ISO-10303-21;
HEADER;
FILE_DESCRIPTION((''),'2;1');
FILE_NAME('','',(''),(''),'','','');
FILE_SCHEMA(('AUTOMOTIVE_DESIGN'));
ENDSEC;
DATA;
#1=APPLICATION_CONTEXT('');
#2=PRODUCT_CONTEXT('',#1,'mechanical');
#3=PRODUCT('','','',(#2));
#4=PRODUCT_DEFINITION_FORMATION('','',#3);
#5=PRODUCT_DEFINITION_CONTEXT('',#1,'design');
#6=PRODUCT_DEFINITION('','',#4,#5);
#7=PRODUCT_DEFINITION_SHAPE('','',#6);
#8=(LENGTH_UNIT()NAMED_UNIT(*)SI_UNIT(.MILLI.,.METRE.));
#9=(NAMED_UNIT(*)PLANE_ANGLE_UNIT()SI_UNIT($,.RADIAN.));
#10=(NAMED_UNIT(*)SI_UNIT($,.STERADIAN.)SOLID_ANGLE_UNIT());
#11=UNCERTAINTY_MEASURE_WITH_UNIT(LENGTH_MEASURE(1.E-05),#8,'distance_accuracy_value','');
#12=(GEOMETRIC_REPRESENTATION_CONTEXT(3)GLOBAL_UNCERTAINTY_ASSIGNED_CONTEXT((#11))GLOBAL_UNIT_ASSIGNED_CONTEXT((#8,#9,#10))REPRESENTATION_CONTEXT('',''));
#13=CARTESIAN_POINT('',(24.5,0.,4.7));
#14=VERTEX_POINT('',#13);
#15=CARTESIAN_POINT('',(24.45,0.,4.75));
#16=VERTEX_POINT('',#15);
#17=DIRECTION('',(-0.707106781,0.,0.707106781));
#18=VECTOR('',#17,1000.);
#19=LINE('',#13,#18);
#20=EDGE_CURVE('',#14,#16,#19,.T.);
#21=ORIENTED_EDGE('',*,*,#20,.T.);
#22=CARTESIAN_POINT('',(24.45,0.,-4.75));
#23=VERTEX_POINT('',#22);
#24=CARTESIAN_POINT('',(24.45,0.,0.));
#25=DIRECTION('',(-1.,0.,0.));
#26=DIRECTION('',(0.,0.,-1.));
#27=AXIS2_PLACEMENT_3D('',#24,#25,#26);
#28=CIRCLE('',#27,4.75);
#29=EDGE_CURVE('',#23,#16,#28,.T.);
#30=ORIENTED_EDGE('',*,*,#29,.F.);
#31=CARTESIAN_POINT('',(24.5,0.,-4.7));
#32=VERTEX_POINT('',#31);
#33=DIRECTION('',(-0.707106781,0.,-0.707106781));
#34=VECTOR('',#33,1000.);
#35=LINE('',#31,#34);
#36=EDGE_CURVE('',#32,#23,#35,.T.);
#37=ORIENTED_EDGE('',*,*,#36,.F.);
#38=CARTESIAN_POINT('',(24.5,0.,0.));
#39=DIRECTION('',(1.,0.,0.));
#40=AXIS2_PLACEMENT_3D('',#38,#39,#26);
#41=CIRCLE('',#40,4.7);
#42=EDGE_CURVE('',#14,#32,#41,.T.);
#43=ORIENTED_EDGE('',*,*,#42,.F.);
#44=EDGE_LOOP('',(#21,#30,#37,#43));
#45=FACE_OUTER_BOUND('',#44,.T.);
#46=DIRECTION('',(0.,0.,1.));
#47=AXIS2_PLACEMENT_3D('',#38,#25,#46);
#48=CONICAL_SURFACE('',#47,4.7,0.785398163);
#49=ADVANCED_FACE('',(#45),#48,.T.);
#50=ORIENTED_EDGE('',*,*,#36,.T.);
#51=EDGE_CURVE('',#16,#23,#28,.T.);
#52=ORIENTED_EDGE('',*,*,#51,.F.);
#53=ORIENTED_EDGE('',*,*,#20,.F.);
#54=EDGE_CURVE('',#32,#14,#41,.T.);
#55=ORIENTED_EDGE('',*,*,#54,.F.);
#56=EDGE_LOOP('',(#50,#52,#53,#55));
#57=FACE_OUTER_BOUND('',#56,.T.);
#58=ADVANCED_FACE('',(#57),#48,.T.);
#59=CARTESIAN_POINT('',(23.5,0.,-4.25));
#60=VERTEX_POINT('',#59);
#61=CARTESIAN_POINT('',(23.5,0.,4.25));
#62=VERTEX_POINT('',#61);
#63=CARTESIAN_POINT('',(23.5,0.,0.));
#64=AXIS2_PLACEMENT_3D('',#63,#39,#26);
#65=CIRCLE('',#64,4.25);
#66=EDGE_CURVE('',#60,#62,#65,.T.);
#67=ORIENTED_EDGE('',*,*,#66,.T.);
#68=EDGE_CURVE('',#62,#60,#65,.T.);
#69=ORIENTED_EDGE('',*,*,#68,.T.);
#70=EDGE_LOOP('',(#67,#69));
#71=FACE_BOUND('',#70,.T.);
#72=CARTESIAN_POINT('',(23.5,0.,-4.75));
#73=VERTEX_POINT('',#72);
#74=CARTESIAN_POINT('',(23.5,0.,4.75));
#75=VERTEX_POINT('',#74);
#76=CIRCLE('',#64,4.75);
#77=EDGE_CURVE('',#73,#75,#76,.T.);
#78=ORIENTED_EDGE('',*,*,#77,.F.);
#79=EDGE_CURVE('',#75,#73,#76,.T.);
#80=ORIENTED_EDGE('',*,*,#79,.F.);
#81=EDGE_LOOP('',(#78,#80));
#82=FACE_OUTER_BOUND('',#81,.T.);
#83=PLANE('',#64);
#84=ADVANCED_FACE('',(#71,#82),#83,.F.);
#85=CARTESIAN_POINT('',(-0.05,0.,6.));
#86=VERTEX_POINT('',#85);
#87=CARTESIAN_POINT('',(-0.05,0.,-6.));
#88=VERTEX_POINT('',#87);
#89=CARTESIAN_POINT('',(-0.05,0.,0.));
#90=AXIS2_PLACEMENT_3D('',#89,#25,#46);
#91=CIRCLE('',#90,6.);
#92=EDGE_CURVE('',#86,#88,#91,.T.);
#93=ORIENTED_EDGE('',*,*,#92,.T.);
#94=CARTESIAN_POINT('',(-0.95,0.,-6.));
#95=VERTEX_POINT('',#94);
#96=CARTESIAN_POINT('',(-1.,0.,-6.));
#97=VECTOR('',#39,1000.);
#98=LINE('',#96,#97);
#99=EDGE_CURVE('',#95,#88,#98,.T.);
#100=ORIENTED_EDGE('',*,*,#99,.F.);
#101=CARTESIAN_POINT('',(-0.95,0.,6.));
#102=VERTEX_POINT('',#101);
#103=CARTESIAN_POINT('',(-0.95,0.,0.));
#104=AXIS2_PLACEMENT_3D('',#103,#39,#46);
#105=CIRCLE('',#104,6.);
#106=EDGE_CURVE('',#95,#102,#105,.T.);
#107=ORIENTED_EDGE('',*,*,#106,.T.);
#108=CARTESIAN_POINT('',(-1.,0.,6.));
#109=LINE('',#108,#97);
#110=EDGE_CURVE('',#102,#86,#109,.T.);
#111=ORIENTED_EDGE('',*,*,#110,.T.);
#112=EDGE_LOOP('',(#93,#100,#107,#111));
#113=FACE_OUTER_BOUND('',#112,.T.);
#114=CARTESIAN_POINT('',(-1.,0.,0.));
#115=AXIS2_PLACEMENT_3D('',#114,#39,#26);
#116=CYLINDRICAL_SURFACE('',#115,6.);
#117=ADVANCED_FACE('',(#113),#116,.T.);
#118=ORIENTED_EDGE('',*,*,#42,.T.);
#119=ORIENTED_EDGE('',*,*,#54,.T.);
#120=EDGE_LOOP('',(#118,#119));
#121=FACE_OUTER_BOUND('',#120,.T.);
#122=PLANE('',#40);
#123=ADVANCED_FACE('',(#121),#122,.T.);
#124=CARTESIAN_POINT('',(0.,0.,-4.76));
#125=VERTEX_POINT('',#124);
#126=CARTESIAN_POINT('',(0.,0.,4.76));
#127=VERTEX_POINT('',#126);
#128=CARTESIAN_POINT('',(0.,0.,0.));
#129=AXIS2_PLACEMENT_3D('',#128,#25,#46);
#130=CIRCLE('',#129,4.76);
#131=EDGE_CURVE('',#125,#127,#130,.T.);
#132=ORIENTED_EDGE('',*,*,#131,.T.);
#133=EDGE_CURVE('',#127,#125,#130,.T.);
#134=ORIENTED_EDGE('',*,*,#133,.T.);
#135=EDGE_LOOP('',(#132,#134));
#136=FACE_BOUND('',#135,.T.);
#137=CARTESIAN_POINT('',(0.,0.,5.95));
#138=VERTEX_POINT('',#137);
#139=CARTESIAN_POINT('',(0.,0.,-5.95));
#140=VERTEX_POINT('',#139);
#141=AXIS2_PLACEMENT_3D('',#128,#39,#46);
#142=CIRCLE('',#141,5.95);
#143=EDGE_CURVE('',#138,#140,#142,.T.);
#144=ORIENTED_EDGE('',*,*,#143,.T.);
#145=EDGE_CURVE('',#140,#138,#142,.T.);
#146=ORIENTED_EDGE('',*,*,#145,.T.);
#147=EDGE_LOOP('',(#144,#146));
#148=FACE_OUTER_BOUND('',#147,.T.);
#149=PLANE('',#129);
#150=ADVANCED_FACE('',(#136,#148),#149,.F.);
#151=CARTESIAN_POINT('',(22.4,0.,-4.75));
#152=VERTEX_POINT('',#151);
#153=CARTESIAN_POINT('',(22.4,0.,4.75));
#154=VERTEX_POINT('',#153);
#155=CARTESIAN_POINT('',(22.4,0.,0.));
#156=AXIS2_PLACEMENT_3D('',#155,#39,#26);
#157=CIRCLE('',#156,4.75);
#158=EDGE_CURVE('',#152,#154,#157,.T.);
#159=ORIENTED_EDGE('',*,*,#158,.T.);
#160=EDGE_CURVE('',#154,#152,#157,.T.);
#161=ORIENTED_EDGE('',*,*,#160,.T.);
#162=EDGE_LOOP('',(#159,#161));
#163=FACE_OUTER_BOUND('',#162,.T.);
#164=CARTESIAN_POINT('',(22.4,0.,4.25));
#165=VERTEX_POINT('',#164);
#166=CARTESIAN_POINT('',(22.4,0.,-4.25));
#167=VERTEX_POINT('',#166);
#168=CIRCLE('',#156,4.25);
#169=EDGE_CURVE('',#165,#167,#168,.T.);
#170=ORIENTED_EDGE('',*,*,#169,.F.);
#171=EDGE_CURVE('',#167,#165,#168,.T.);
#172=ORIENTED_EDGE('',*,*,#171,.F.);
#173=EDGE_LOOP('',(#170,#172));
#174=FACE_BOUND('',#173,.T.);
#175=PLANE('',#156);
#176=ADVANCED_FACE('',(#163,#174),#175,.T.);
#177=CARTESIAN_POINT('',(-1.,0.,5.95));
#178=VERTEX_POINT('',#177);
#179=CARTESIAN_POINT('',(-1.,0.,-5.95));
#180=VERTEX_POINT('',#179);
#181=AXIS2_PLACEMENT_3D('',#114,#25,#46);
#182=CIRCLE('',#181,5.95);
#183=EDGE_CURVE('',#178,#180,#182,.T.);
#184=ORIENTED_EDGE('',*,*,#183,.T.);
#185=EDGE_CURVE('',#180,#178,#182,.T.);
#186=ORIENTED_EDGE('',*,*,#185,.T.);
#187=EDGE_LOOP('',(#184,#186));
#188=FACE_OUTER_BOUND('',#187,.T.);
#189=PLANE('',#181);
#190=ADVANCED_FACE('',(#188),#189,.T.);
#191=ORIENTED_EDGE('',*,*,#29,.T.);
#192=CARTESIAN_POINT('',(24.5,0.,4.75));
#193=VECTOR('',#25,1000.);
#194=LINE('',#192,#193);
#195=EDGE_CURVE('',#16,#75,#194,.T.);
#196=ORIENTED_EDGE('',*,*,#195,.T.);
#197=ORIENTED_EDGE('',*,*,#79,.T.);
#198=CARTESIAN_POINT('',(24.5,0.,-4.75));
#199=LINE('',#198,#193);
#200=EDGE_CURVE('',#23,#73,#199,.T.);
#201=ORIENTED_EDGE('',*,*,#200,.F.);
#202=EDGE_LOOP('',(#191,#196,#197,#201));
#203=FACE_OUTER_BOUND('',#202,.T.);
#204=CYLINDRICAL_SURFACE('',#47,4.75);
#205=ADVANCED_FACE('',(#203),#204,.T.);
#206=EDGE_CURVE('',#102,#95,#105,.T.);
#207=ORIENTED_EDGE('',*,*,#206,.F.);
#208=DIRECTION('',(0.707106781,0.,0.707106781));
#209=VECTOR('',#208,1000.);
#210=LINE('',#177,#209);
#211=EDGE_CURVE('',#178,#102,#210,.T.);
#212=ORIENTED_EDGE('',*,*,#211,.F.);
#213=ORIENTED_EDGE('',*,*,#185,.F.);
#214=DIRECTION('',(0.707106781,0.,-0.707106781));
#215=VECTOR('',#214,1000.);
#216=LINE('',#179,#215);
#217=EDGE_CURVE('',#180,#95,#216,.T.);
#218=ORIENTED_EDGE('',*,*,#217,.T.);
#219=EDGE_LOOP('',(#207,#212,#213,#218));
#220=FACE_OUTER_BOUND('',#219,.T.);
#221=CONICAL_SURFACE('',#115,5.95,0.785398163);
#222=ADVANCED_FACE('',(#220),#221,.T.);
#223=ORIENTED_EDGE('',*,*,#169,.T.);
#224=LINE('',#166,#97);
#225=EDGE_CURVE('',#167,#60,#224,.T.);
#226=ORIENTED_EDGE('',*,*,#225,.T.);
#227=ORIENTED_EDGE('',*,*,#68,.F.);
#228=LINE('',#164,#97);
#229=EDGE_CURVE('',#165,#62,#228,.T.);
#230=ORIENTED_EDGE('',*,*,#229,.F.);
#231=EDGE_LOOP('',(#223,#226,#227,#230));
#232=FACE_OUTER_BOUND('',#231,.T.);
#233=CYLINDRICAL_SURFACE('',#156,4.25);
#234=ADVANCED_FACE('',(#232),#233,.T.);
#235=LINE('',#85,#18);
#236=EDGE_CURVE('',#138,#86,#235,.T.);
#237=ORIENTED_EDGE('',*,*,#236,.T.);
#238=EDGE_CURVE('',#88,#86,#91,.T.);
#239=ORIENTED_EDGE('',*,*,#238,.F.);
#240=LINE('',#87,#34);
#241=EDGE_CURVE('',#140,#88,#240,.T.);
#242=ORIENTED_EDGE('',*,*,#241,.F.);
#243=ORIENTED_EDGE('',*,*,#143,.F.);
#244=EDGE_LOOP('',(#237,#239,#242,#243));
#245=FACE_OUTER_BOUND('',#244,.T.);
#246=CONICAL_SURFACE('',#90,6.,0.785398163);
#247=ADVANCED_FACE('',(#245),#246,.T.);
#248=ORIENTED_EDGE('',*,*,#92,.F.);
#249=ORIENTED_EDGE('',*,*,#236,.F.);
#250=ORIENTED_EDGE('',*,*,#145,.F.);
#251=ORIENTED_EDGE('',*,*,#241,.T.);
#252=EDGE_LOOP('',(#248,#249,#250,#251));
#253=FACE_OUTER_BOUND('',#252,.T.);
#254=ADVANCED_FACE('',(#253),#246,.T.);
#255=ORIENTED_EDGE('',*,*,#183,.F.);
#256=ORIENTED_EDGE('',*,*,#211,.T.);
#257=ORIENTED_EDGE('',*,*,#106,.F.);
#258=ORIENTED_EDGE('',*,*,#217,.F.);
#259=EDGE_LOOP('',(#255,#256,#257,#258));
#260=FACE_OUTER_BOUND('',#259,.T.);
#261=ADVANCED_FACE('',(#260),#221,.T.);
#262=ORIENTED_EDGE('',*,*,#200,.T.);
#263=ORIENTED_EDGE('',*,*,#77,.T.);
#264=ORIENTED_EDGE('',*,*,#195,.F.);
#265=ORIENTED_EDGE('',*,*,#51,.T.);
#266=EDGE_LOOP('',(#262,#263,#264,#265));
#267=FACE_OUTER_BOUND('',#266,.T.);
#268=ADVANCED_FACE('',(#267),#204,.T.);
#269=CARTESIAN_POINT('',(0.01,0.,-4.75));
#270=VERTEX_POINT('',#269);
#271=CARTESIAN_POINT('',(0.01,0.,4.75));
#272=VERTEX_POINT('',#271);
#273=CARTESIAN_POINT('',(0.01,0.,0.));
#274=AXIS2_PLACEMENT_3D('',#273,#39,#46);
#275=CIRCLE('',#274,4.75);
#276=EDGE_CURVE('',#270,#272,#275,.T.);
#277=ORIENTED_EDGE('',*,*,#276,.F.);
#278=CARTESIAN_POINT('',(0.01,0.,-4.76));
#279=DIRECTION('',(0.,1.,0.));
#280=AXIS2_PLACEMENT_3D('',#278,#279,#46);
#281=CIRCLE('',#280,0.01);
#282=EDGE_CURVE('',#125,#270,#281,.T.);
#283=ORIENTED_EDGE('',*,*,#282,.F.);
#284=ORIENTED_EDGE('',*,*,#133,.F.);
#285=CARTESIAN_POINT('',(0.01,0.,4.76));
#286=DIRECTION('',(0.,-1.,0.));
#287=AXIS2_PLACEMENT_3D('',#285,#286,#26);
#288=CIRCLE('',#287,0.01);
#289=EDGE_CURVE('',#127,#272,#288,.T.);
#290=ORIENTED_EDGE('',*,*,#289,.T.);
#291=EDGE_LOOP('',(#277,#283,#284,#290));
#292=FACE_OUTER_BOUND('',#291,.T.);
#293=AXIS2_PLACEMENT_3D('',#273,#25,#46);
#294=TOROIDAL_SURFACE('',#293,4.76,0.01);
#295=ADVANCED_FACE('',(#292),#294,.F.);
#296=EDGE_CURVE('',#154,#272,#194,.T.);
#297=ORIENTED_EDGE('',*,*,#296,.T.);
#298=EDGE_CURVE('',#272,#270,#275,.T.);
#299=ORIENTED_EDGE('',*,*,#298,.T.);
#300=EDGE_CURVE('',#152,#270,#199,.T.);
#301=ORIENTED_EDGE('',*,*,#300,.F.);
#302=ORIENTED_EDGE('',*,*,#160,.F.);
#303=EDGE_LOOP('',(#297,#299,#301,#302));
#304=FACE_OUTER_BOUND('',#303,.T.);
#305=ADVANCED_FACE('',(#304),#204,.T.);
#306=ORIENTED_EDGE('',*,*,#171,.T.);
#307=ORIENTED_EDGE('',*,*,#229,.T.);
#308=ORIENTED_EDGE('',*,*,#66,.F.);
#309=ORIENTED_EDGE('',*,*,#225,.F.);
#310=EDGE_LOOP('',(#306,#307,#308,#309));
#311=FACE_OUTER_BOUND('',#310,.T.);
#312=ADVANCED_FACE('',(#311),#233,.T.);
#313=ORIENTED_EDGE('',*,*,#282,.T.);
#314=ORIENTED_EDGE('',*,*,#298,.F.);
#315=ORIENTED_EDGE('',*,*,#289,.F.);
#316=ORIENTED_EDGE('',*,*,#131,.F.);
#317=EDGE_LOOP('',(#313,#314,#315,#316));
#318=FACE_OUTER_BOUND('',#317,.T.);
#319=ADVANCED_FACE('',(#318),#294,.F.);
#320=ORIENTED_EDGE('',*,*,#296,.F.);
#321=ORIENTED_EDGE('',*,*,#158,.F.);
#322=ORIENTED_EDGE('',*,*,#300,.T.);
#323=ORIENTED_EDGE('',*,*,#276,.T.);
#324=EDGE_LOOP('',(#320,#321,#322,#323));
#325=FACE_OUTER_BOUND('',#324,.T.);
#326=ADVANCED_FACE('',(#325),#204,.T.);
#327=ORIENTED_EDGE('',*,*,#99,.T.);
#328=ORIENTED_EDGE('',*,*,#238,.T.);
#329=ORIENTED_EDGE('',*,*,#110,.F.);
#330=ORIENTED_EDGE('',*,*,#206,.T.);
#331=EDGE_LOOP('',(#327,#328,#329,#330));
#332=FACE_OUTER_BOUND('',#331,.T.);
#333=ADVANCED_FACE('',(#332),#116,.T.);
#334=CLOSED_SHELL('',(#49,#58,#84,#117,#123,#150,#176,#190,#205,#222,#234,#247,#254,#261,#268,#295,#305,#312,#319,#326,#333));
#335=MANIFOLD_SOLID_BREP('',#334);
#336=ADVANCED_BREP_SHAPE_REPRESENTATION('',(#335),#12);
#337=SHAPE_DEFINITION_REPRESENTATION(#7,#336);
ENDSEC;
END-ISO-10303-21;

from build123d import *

# Parameters (mm, degrees)
SKETCH1_R           = 4.75
BOSS_EXTRUDE1_DEPTH = 24.5
SKETCH2_R           = 6
BOSS_EXTRUDE2_DEPTH = 1
CHAMFER1_SIZE       = 0.05
FILLET1_R           = 0.01
CHAMFER2_SIZE       = 0.05
SKETCH4_R           = 5.5
SKETCH4_R_2         = 4.25
CUT_EXTRUDE1_DEPTH  = 1.1


with BuildPart() as part:
    # Sketch1 → Boss-Extrude1 (new body)
    with BuildSketch(Plane(origin=(0, 0, 0), x_dir=(0, 0, -1), z_dir=(1, 0, 0))):
        Circle(SKETCH1_R)
    extrude(amount=BOSS_EXTRUDE1_DEPTH)

    # Sketch2 → Boss-Extrude2 (add)
    with BuildSketch(Plane.ZY):
        Circle(SKETCH2_R)
    extrude(amount=BOSS_EXTRUDE2_DEPTH)

    # Chamfer1
    chamfer1_edges = [part.edges().sort_by_distance(p)[0] for p in [
        (0, 0, -6),
        (-1, 0, -6),
    ]]
    chamfer(chamfer1_edges, length=CHAMFER1_SIZE)

    # Fillet1
    fillet1_edges = [part.edges().sort_by_distance(p)[0] for p in [
        (0, 0, 4.75),
    ]]
    fillet(fillet1_edges, radius=FILLET1_R)

    # Chamfer2
    chamfer2_edges = [part.edges().sort_by_distance(p)[0] for p in [
        (24.5, 0, 4.75),
    ]]
    chamfer(chamfer2_edges, length=CHAMFER2_SIZE)

    # Sketch4 → Cut-Extrude1 (cut)
    with BuildSketch(Plane(origin=(23.5, 0, 0), x_dir=(0, 0, -1), z_dir=(1, 0, 0))):
        Circle(SKETCH4_R)
        Circle(SKETCH4_R_2, mode=Mode.SUBTRACT)
    extrude(amount=-CUT_EXTRUDE1_DEPTH, mode=Mode.SUBTRACT)


solid = part.part
